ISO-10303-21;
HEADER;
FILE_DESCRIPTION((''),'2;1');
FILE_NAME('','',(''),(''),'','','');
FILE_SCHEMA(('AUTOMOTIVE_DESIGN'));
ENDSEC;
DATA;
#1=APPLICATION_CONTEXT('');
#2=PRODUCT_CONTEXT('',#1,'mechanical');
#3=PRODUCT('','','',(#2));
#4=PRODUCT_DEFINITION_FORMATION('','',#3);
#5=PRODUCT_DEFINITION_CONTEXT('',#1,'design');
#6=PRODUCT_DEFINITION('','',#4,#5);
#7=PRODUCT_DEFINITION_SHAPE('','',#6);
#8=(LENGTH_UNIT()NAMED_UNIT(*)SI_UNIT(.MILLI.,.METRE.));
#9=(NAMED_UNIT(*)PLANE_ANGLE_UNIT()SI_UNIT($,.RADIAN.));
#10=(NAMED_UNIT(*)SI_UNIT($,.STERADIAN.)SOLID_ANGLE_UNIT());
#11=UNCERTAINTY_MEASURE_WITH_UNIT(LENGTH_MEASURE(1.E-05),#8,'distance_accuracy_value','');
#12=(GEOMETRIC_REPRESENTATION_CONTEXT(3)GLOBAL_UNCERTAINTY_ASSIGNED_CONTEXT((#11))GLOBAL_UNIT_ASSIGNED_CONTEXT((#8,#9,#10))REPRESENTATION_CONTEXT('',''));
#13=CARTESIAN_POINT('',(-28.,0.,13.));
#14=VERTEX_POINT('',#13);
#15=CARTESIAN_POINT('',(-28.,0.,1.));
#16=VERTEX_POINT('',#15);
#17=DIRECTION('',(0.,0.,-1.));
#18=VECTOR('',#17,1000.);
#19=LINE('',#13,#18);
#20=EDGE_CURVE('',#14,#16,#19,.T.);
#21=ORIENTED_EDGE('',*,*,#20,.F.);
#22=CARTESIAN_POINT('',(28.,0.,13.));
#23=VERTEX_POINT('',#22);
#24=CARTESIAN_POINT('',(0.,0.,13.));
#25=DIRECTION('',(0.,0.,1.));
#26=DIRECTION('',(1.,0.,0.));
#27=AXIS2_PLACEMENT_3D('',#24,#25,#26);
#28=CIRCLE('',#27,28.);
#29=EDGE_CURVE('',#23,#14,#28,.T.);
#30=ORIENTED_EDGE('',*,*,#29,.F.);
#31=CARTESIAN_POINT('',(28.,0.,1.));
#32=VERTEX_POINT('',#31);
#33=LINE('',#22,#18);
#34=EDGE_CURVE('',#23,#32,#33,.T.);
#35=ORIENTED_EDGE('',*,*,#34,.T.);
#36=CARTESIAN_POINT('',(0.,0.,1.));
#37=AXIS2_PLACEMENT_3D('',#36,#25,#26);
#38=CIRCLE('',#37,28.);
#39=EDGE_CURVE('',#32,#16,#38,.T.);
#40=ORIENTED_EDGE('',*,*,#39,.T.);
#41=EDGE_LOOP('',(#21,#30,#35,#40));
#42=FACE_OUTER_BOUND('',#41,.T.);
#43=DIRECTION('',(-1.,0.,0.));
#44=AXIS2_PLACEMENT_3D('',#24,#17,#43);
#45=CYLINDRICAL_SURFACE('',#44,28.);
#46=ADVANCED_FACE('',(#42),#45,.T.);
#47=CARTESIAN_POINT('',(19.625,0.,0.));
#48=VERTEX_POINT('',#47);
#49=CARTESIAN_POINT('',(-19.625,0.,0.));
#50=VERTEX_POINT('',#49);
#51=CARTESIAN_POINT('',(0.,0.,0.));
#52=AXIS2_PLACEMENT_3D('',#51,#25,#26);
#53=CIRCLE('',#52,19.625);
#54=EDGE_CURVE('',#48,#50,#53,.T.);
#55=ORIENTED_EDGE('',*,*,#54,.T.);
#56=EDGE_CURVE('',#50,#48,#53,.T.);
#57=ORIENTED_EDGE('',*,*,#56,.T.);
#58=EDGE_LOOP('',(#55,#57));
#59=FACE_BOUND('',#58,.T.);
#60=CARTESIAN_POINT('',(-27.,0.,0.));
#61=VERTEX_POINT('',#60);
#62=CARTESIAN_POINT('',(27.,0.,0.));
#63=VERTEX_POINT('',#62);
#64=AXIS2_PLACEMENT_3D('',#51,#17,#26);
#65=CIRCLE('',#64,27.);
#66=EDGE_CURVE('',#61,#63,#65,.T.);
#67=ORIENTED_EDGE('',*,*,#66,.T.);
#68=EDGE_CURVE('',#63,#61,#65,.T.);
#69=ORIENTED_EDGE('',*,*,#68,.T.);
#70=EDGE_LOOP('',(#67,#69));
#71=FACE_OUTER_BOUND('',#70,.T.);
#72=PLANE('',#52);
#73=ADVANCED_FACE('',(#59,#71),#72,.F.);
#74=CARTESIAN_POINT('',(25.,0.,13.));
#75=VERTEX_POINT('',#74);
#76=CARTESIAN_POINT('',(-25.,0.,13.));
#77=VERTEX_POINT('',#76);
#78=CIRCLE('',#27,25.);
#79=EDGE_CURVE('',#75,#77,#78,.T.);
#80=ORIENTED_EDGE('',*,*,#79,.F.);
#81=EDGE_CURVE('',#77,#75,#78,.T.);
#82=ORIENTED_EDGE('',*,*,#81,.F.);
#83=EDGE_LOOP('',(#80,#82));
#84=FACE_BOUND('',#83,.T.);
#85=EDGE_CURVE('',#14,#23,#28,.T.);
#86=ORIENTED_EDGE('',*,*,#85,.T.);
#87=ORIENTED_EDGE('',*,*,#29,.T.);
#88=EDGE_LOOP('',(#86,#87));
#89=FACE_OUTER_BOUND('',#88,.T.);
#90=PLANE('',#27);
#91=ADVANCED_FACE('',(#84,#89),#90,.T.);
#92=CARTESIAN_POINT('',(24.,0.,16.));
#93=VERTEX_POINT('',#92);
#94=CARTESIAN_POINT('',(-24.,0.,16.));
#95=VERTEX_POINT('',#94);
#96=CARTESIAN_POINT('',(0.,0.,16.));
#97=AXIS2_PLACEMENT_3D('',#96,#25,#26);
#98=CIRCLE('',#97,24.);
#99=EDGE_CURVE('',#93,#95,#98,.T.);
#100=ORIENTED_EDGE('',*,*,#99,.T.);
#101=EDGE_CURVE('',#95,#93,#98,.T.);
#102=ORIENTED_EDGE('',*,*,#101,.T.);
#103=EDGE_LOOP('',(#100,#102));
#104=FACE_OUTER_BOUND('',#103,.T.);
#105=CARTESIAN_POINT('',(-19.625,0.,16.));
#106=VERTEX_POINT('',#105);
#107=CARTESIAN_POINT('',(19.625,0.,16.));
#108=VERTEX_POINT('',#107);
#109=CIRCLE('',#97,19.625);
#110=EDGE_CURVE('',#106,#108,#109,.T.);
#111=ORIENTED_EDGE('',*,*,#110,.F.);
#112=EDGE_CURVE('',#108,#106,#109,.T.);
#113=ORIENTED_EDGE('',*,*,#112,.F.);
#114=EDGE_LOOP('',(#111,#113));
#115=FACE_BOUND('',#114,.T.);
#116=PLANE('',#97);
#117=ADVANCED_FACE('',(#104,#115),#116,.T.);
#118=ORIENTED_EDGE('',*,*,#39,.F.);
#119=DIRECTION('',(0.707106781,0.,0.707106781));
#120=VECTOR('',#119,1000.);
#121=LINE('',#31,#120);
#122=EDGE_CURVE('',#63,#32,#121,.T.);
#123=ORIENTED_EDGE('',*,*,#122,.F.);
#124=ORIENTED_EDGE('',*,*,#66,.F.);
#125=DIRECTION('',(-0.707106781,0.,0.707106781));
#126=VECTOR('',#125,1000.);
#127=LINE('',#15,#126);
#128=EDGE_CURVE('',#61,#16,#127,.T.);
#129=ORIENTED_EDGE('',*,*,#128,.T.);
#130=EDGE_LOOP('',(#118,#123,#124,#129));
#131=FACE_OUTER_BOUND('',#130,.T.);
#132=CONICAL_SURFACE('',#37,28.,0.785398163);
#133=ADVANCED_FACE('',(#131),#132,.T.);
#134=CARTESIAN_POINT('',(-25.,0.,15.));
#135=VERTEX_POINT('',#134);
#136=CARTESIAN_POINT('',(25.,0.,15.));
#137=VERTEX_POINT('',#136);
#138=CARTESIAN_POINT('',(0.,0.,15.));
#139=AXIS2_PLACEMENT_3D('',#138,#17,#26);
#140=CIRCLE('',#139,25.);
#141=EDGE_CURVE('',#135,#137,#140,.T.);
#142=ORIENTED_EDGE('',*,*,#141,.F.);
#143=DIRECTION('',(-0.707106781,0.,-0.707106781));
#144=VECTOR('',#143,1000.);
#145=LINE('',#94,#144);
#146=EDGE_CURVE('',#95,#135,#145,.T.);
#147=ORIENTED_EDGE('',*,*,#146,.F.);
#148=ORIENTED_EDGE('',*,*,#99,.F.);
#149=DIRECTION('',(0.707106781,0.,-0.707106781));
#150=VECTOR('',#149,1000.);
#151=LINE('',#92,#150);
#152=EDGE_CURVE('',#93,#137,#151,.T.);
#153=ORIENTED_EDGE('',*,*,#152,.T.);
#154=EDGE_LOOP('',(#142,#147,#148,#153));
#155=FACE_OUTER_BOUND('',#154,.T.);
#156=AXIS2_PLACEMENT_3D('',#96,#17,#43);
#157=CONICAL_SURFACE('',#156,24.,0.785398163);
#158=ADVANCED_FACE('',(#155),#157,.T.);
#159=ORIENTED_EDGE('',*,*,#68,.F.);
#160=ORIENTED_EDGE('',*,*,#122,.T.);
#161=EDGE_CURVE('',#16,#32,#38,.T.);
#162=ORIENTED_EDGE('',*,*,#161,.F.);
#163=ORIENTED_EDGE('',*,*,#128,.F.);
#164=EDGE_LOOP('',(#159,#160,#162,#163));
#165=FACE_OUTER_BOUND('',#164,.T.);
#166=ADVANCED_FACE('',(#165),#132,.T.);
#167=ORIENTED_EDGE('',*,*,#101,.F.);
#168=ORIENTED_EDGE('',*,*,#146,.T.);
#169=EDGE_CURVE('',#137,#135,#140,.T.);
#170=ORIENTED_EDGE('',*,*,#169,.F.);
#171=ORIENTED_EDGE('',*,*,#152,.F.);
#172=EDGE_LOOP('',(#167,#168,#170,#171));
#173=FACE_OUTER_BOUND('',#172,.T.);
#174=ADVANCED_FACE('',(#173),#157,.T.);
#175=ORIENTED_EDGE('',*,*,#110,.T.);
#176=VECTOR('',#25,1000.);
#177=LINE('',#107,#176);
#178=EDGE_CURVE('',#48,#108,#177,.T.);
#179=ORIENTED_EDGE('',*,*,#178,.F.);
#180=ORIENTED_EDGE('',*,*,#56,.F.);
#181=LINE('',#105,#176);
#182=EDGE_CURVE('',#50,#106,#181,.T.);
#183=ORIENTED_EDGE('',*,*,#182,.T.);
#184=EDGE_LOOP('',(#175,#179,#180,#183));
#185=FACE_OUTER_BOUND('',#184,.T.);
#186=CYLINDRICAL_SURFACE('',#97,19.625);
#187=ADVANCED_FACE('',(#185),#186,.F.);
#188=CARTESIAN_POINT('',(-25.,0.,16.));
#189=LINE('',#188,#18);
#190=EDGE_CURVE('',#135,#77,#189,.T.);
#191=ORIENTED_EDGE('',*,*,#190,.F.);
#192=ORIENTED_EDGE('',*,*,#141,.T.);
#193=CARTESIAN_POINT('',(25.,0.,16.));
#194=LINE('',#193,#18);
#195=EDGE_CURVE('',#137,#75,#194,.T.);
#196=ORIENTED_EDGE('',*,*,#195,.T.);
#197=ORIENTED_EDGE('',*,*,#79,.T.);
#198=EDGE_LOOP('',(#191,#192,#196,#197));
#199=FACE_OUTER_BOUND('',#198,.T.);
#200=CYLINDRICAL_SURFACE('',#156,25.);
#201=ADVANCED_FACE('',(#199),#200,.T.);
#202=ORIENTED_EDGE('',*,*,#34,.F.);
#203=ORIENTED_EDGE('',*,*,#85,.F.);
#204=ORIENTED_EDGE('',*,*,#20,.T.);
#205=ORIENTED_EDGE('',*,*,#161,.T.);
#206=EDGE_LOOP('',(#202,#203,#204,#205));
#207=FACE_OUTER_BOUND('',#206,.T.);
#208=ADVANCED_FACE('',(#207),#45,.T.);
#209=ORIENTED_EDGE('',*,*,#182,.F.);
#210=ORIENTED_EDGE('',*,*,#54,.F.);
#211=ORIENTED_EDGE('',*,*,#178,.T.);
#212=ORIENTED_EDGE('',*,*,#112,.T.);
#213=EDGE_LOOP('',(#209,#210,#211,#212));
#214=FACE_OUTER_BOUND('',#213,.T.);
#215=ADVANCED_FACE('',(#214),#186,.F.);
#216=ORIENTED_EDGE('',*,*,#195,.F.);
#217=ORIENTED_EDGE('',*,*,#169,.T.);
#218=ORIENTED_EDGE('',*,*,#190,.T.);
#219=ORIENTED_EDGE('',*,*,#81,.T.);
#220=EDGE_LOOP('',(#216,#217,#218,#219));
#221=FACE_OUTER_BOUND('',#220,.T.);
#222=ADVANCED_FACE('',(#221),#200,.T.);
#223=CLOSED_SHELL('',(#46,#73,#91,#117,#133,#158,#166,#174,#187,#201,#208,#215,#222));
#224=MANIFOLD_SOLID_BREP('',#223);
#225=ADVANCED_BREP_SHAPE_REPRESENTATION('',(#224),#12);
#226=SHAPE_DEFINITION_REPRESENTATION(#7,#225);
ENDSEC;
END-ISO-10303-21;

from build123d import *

# Parameters (mm, degrees)
SKETCH1_R           = 28
BOSS_EXTRUDE1_DEPTH = 13
SKETCH2_R           = 25
BOSS_EXTRUDE2_DEPTH = 3
CHAMFER1_SIZE       = 1


with BuildPart() as part:
    # Sketch1 → Boss-Extrude1 (new body)
    with BuildSketch(Plane.XY):
        with Locations(Location((0, 0, 0), (0, 0, 180))):
            Circle(SKETCH1_R)
    extrude(amount=BOSS_EXTRUDE1_DEPTH)

    # Sketch2 → Boss-Extrude2 (add)
    with BuildSketch(Plane.XY.offset(13)):
        Circle(SKETCH2_R)
    extrude(amount=BOSS_EXTRUDE2_DEPTH)

    # Chamfer1
    chamfer1_edges = [part.edges().sort_by_distance(p)[0] for p in [
        (28, 0, 0),
        (-25, 0, 16),
    ]]
    chamfer(chamfer1_edges, length=CHAMFER1_SIZE)

    # Sketch4 → G1-1/4 Tapped Hole1 (revolve, cut)
    with BuildSketch(Plane(origin=(0, 0, 16), x_dir=(0, -1, 0), z_dir=(1, 0, 0))):
        Polygon((0, 0), (0, 102.538889648), (19.625, 90.747), (19.625, 0), align=None)
    revolve(axis=Axis((0, 0, 22.35), (0, 0, -1)), mode=Mode.SUBTRACT)


solid = part.part
